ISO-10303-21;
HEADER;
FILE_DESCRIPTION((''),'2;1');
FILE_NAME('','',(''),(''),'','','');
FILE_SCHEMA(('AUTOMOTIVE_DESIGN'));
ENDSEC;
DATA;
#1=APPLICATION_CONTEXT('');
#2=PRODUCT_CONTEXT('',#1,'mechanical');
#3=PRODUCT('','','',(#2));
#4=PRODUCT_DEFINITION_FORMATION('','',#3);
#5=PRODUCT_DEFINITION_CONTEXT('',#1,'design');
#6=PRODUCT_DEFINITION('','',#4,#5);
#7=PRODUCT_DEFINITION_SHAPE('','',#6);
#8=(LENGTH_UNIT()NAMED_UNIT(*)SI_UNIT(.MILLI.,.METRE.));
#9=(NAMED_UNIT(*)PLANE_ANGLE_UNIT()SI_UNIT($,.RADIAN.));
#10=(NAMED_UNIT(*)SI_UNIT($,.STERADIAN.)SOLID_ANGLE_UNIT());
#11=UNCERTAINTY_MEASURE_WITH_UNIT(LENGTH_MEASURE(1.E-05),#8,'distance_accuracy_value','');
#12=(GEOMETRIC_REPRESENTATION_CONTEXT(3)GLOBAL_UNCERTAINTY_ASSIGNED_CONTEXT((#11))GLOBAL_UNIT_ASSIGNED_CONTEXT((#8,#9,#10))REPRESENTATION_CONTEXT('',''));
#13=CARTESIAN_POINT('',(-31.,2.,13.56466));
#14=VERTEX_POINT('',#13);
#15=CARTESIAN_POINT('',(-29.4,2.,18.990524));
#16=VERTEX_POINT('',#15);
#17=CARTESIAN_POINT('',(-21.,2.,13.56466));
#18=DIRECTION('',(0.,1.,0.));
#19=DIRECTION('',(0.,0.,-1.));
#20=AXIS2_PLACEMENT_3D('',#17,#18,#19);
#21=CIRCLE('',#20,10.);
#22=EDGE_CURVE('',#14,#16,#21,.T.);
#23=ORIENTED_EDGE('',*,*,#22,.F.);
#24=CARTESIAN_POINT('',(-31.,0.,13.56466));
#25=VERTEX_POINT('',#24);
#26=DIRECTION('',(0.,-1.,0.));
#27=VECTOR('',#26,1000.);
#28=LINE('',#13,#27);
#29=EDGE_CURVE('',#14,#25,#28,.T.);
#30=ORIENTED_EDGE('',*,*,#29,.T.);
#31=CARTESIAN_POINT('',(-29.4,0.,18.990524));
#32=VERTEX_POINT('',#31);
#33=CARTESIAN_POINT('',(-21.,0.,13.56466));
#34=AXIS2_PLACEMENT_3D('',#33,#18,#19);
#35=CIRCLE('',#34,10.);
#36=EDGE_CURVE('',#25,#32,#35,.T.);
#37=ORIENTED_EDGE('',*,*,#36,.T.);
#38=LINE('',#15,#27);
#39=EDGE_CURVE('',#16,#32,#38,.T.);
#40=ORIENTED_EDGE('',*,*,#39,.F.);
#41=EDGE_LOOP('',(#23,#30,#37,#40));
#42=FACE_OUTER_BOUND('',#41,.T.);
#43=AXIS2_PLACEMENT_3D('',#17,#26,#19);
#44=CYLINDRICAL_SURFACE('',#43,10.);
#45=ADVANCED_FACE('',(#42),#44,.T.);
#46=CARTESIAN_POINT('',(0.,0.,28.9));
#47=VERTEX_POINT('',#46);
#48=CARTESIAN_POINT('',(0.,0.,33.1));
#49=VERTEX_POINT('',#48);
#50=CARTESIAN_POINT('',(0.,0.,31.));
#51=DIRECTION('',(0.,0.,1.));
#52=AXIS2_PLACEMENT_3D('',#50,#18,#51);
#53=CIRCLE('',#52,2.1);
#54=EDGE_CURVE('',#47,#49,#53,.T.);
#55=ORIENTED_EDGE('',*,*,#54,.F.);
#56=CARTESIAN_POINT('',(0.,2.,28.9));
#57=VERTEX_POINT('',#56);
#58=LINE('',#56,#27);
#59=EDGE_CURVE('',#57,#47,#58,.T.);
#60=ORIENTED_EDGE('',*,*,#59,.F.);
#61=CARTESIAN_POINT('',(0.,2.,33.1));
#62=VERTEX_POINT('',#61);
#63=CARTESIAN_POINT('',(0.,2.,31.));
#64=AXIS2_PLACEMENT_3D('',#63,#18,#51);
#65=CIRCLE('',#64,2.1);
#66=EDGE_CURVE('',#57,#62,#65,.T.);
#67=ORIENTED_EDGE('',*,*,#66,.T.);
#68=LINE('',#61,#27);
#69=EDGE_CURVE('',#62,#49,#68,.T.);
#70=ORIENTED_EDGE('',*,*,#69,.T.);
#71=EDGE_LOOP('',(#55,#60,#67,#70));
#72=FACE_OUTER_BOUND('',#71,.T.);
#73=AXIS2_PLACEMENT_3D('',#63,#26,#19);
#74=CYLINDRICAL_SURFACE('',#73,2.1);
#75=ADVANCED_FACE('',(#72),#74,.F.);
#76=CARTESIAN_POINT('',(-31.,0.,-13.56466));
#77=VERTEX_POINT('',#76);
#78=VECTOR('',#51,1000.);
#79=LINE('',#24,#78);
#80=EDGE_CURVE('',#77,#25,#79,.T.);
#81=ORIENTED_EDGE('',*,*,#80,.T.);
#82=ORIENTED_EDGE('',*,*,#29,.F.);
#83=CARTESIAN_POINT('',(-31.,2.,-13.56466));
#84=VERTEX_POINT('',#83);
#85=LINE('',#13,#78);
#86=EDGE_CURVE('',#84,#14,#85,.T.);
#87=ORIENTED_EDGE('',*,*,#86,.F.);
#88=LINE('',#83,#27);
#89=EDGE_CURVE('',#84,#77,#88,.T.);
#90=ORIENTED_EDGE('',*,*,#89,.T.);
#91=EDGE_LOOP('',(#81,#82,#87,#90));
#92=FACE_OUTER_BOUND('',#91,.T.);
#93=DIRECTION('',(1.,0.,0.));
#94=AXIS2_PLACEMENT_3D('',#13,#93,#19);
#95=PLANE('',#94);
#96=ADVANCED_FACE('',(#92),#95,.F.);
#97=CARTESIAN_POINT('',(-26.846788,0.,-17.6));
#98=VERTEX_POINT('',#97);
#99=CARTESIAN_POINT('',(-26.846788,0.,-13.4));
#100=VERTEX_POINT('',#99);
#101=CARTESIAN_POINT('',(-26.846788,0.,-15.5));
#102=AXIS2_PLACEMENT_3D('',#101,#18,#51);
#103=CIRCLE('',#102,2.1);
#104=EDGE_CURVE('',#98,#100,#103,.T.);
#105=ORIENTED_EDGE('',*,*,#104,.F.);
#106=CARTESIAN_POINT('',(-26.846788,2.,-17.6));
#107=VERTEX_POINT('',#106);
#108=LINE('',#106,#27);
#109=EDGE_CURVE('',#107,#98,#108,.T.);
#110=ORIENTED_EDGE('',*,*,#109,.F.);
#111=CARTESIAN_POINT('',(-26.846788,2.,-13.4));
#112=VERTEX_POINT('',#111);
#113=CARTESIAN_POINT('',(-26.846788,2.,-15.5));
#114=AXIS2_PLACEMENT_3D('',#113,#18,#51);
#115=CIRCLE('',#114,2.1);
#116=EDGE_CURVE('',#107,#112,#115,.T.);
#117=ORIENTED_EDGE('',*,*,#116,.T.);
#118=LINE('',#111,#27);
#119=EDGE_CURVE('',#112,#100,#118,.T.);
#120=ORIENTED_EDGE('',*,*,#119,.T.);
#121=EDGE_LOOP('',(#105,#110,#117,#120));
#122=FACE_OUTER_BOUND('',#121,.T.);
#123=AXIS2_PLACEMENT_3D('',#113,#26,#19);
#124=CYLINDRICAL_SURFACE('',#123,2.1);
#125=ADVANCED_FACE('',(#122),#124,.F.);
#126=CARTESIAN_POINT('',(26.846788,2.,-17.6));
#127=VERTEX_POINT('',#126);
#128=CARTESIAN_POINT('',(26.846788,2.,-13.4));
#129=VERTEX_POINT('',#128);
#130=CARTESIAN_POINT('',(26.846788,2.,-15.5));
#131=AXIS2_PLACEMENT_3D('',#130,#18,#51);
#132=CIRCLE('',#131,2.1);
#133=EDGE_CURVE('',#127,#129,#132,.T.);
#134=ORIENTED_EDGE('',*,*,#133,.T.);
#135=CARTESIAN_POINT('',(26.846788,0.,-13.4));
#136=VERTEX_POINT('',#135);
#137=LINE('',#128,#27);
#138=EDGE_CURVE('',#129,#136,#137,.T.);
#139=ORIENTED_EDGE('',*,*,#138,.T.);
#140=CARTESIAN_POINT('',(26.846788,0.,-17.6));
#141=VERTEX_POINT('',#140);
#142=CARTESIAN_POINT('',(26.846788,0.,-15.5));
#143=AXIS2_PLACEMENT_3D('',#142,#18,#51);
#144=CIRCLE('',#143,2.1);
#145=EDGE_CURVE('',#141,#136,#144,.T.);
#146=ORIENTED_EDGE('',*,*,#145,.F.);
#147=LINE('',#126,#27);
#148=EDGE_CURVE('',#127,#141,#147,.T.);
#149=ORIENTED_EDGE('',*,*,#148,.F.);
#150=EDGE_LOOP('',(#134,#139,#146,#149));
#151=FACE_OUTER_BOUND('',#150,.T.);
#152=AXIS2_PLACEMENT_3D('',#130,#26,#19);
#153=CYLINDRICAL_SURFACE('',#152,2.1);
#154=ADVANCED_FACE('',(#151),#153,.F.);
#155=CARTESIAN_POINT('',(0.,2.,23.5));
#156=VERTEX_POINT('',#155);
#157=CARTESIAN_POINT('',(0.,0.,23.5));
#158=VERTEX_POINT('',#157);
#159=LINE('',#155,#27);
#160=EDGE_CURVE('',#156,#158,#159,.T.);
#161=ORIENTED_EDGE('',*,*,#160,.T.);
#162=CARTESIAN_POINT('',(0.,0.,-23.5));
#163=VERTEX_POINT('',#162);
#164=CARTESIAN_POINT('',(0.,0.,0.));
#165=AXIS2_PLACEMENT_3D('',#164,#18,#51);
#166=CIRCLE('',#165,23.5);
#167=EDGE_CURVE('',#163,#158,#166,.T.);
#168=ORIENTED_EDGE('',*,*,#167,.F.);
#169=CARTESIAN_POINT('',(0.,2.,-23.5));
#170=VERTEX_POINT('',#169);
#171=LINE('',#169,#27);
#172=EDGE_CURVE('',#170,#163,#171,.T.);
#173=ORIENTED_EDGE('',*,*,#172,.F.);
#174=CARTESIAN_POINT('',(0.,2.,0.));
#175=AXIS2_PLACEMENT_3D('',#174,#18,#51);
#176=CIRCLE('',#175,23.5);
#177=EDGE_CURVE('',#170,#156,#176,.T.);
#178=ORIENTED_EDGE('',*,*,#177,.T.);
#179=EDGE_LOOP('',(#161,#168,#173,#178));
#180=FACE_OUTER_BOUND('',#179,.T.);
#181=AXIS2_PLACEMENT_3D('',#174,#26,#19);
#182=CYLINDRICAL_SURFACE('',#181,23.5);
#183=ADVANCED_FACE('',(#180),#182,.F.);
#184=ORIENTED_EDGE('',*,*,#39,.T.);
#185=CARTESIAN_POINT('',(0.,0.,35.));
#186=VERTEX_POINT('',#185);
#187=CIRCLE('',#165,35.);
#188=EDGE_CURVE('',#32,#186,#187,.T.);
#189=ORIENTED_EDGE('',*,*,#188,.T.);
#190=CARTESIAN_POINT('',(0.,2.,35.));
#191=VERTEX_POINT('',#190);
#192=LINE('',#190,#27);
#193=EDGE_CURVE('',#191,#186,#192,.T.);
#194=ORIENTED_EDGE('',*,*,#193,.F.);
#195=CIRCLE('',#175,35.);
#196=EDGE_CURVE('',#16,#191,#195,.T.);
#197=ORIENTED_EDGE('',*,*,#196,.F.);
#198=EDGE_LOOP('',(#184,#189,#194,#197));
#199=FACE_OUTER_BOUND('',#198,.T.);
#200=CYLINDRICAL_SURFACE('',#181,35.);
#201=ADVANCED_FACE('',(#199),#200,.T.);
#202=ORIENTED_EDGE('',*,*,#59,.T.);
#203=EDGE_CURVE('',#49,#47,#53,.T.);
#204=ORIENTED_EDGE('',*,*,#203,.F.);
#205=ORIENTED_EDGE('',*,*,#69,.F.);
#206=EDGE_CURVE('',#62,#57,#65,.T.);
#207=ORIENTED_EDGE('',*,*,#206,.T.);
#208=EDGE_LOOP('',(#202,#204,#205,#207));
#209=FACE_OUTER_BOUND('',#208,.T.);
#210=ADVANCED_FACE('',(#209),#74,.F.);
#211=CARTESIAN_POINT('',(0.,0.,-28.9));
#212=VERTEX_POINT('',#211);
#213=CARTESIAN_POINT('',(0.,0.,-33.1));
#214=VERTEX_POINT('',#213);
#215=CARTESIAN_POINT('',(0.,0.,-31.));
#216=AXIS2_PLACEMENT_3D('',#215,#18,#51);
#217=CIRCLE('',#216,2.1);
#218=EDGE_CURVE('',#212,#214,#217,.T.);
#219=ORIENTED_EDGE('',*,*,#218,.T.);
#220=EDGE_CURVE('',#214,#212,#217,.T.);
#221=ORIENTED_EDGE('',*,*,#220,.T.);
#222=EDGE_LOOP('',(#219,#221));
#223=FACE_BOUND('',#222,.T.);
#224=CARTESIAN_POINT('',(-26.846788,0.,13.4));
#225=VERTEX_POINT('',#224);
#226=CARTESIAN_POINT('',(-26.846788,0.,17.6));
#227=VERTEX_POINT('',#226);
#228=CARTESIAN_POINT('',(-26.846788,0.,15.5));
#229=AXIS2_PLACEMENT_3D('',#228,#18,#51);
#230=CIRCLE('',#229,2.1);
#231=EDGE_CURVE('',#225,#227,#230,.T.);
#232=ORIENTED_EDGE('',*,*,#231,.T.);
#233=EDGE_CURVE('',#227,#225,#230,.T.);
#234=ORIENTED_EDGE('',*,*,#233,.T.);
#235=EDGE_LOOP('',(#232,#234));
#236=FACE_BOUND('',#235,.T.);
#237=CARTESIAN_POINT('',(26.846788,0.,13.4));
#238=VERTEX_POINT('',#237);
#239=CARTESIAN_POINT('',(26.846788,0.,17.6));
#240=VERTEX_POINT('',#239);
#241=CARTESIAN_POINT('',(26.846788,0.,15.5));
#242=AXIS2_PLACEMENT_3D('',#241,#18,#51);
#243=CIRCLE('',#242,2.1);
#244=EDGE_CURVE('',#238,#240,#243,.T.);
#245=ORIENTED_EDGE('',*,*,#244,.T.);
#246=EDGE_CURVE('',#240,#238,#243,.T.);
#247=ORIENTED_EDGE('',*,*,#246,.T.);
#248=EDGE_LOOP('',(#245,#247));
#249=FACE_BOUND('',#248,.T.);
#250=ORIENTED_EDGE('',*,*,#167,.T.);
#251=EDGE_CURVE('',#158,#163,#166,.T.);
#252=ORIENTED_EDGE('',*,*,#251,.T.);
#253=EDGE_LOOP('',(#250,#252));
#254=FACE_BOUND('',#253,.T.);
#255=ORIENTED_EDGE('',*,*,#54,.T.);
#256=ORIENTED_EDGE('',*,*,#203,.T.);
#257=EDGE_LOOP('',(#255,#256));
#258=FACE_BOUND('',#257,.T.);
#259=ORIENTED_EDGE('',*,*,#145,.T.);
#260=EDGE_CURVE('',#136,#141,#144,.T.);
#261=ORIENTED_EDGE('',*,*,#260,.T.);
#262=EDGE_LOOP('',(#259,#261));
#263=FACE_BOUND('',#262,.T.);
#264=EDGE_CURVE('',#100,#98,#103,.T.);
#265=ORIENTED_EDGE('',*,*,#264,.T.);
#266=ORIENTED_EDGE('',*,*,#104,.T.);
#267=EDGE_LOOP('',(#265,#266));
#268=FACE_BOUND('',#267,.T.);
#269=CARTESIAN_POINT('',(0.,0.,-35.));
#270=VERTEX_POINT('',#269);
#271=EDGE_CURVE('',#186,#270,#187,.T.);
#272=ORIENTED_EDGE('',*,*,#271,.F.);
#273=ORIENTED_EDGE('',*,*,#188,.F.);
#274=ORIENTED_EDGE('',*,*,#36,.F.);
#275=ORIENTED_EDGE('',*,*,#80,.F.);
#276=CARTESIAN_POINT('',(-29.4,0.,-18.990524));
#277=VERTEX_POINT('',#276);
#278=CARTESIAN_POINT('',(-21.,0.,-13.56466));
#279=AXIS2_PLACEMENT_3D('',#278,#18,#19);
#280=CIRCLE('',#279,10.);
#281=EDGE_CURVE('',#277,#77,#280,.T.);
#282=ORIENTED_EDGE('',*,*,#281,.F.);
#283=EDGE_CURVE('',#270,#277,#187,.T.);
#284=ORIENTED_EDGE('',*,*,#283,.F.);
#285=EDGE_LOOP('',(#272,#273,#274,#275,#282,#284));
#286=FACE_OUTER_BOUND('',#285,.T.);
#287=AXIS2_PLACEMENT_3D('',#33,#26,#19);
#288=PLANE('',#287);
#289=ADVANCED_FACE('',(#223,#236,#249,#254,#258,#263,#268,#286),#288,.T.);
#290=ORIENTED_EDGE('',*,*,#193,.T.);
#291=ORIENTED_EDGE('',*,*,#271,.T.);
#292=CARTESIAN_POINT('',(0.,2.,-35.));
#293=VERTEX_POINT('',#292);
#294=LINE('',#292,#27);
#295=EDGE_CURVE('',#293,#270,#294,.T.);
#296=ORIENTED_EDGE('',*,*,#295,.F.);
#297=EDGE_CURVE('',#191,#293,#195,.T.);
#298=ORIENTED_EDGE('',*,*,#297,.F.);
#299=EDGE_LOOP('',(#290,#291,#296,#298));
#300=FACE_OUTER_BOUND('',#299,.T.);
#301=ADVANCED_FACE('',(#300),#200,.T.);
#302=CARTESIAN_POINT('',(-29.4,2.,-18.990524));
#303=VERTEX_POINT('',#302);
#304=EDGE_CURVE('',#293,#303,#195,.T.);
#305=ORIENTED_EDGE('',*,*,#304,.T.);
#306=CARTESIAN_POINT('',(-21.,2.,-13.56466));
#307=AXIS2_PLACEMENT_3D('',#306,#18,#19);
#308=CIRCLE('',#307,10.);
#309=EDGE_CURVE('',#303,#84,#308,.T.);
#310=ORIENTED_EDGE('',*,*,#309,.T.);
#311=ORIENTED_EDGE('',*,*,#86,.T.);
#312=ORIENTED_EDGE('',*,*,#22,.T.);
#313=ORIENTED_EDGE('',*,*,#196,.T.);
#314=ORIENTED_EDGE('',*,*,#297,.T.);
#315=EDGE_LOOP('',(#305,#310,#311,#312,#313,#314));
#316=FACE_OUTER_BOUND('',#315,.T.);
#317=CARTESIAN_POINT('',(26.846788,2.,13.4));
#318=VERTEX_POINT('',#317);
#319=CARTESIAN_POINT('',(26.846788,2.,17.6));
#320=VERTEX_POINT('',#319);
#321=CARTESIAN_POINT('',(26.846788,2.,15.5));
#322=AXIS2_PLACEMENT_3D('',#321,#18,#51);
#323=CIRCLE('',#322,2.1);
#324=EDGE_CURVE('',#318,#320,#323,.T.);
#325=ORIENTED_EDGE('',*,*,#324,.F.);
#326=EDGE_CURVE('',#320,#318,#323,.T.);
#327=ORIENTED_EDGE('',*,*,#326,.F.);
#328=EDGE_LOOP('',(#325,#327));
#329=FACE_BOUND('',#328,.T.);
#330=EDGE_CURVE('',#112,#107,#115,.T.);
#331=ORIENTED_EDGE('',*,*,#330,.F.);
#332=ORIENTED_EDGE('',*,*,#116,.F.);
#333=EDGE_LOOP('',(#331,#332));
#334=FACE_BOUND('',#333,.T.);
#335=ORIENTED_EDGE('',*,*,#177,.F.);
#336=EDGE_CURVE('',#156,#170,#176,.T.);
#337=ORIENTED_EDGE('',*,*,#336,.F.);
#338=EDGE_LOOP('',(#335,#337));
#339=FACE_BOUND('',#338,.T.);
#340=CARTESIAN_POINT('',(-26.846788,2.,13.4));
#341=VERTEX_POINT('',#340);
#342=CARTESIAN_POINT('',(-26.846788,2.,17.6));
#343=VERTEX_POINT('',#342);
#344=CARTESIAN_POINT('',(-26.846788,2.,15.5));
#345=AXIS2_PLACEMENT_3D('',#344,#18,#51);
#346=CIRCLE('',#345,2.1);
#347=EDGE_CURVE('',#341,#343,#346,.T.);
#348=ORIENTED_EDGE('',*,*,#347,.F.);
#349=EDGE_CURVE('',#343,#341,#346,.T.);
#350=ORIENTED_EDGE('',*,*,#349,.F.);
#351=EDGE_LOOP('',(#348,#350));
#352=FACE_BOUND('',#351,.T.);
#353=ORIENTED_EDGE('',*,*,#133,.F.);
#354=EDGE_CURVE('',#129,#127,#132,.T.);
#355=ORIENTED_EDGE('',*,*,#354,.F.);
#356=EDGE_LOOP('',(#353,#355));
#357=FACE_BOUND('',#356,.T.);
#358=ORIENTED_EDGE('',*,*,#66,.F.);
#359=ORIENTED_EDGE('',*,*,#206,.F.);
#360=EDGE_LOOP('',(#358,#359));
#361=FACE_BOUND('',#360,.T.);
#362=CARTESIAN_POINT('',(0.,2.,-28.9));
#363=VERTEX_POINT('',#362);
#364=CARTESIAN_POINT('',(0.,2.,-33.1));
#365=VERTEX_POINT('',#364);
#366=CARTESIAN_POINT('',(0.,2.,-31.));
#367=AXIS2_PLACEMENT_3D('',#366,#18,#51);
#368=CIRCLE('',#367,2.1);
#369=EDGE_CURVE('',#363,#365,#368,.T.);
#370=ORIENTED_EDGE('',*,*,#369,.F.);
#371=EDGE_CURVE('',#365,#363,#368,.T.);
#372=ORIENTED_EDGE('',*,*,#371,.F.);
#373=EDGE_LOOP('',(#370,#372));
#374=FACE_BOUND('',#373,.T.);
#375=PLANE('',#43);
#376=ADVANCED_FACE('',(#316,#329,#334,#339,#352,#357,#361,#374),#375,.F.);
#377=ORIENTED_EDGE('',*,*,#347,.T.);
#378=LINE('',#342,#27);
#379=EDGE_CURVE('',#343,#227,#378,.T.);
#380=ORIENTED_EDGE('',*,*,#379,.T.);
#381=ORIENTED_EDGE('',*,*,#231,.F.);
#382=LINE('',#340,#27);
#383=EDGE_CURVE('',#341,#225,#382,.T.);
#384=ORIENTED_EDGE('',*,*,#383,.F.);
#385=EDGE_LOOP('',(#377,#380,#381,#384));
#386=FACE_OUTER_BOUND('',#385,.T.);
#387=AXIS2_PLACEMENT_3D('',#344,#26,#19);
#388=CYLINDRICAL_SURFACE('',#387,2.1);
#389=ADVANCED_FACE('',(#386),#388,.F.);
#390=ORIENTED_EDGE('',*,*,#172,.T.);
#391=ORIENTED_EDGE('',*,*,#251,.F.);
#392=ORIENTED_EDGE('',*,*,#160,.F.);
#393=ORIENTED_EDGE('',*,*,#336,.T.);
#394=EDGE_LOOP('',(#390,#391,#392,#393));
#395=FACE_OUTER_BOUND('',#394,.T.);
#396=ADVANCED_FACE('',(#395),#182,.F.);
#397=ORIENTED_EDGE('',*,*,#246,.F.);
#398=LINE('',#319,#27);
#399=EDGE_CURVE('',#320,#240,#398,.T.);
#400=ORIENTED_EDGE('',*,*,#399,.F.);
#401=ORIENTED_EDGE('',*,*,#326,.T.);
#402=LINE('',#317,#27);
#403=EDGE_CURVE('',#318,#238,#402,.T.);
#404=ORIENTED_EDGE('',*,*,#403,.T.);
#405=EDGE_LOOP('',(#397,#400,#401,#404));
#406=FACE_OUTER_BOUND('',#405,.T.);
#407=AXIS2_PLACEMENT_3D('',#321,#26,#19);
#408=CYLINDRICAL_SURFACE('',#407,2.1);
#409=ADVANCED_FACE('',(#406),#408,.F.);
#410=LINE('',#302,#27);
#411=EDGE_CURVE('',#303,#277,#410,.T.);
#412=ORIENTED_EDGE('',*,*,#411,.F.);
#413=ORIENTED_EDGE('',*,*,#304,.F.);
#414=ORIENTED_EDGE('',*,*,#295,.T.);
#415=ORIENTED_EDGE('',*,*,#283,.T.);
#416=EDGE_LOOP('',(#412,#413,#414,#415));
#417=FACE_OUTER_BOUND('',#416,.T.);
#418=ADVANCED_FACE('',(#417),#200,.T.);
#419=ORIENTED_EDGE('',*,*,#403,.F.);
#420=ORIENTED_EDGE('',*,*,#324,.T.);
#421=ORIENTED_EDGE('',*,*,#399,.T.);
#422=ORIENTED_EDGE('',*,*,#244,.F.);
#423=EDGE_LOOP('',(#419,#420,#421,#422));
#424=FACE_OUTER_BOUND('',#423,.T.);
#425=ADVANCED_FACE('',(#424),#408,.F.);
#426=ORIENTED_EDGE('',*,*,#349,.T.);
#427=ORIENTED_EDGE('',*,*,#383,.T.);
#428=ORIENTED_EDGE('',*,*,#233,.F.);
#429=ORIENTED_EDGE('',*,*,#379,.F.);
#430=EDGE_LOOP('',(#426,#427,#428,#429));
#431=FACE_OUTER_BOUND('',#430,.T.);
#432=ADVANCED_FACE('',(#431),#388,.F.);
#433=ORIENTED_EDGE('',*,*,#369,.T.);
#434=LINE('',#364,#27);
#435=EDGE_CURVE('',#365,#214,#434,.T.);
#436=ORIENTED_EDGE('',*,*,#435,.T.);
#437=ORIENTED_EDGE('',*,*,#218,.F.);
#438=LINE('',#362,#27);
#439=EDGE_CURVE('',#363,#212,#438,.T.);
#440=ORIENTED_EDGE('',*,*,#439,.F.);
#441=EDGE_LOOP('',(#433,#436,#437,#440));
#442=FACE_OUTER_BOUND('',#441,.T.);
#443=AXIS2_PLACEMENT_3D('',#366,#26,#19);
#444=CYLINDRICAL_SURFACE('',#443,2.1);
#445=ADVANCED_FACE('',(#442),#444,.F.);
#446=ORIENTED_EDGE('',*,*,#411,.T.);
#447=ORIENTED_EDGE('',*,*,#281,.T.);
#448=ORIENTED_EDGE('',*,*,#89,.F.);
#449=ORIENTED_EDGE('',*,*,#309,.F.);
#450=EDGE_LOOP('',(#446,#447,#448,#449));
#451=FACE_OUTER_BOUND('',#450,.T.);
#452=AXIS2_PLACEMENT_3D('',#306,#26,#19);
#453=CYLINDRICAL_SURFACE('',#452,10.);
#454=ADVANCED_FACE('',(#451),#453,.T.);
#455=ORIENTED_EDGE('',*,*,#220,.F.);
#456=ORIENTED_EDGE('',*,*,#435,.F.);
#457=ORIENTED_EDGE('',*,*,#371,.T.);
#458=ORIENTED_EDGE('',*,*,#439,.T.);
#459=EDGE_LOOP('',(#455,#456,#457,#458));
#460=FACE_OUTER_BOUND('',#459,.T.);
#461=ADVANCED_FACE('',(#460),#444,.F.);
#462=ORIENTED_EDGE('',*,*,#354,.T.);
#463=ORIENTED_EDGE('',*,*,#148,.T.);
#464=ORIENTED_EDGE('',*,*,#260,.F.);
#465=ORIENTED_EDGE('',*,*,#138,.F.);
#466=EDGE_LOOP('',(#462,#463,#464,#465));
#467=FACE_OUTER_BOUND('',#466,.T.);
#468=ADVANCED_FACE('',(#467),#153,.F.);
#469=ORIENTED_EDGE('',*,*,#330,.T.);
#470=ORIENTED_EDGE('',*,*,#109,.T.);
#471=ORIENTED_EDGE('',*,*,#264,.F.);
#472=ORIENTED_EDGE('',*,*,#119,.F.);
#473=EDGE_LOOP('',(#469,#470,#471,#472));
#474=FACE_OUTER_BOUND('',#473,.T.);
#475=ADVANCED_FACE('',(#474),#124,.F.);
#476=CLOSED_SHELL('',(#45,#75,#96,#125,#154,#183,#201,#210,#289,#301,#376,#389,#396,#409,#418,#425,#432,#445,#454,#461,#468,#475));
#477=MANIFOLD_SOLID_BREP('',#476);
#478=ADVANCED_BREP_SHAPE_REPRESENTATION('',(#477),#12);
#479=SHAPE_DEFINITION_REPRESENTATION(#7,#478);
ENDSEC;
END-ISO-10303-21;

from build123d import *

# Parameters (mm, degrees)
SKETCH_1_R      = 23.5
SKETCH_1_R_2    = 2.1
EXTRUDE_1_DEPTH = 2


with BuildPart() as part:
    # 草图1 → 凸台-拉伸1 (new body)
    with BuildSketch(Plane(origin=(0, 0, 0), x_dir=(1, 0, 0), z_dir=(0, 1, 0))):
        with BuildLine():
            Line((-31, -13.564659966), (-31, 13.564659966))
            ThreePointArc((-31, 13.564659966), (-30.591663047, 16.393087091), (-29.4, 18.990523953))
            ThreePointArc((-29.4, 18.990523953), (35, 0), (-29.4, -18.990523953))
            ThreePointArc((-29.4, -18.990523953), (-30.591663047, -16.393087091), (-31, -13.564659966))
        make_face()
        with Locations(Location((0, 0, 0), (0, 0, 270))):
            Circle(SKETCH_1_R, mode=Mode.SUBTRACT)
        with Locations(Location((0, 31, 0), (0, 0, 270))):
            Circle(SKETCH_1_R_2, mode=Mode.SUBTRACT)
        with Locations(Location((26.846787517, 15.5, 0), (0, 0, 270))):
            Circle(SKETCH_1_R_2, mode=Mode.SUBTRACT)
        with Locations(Location((26.846787517, -15.5, 0), (0, 0, 270))):
            Circle(SKETCH_1_R_2, mode=Mode.SUBTRACT)
        with Locations(Location((0, -31, 0), (0, 0, 270))):
            Circle(SKETCH_1_R_2, mode=Mode.SUBTRACT)
        with Locations(Location((-26.846787517, -15.5, 0), (0, 0, 270))):
            Circle(SKETCH_1_R_2, mode=Mode.SUBTRACT)
        with Locations(Location((-26.846787517, 15.5, 0), (0, 0, 270))):
            Circle(SKETCH_1_R_2, mode=Mode.SUBTRACT)
    extrude(amount=EXTRUDE_1_DEPTH)


solid = part.part
